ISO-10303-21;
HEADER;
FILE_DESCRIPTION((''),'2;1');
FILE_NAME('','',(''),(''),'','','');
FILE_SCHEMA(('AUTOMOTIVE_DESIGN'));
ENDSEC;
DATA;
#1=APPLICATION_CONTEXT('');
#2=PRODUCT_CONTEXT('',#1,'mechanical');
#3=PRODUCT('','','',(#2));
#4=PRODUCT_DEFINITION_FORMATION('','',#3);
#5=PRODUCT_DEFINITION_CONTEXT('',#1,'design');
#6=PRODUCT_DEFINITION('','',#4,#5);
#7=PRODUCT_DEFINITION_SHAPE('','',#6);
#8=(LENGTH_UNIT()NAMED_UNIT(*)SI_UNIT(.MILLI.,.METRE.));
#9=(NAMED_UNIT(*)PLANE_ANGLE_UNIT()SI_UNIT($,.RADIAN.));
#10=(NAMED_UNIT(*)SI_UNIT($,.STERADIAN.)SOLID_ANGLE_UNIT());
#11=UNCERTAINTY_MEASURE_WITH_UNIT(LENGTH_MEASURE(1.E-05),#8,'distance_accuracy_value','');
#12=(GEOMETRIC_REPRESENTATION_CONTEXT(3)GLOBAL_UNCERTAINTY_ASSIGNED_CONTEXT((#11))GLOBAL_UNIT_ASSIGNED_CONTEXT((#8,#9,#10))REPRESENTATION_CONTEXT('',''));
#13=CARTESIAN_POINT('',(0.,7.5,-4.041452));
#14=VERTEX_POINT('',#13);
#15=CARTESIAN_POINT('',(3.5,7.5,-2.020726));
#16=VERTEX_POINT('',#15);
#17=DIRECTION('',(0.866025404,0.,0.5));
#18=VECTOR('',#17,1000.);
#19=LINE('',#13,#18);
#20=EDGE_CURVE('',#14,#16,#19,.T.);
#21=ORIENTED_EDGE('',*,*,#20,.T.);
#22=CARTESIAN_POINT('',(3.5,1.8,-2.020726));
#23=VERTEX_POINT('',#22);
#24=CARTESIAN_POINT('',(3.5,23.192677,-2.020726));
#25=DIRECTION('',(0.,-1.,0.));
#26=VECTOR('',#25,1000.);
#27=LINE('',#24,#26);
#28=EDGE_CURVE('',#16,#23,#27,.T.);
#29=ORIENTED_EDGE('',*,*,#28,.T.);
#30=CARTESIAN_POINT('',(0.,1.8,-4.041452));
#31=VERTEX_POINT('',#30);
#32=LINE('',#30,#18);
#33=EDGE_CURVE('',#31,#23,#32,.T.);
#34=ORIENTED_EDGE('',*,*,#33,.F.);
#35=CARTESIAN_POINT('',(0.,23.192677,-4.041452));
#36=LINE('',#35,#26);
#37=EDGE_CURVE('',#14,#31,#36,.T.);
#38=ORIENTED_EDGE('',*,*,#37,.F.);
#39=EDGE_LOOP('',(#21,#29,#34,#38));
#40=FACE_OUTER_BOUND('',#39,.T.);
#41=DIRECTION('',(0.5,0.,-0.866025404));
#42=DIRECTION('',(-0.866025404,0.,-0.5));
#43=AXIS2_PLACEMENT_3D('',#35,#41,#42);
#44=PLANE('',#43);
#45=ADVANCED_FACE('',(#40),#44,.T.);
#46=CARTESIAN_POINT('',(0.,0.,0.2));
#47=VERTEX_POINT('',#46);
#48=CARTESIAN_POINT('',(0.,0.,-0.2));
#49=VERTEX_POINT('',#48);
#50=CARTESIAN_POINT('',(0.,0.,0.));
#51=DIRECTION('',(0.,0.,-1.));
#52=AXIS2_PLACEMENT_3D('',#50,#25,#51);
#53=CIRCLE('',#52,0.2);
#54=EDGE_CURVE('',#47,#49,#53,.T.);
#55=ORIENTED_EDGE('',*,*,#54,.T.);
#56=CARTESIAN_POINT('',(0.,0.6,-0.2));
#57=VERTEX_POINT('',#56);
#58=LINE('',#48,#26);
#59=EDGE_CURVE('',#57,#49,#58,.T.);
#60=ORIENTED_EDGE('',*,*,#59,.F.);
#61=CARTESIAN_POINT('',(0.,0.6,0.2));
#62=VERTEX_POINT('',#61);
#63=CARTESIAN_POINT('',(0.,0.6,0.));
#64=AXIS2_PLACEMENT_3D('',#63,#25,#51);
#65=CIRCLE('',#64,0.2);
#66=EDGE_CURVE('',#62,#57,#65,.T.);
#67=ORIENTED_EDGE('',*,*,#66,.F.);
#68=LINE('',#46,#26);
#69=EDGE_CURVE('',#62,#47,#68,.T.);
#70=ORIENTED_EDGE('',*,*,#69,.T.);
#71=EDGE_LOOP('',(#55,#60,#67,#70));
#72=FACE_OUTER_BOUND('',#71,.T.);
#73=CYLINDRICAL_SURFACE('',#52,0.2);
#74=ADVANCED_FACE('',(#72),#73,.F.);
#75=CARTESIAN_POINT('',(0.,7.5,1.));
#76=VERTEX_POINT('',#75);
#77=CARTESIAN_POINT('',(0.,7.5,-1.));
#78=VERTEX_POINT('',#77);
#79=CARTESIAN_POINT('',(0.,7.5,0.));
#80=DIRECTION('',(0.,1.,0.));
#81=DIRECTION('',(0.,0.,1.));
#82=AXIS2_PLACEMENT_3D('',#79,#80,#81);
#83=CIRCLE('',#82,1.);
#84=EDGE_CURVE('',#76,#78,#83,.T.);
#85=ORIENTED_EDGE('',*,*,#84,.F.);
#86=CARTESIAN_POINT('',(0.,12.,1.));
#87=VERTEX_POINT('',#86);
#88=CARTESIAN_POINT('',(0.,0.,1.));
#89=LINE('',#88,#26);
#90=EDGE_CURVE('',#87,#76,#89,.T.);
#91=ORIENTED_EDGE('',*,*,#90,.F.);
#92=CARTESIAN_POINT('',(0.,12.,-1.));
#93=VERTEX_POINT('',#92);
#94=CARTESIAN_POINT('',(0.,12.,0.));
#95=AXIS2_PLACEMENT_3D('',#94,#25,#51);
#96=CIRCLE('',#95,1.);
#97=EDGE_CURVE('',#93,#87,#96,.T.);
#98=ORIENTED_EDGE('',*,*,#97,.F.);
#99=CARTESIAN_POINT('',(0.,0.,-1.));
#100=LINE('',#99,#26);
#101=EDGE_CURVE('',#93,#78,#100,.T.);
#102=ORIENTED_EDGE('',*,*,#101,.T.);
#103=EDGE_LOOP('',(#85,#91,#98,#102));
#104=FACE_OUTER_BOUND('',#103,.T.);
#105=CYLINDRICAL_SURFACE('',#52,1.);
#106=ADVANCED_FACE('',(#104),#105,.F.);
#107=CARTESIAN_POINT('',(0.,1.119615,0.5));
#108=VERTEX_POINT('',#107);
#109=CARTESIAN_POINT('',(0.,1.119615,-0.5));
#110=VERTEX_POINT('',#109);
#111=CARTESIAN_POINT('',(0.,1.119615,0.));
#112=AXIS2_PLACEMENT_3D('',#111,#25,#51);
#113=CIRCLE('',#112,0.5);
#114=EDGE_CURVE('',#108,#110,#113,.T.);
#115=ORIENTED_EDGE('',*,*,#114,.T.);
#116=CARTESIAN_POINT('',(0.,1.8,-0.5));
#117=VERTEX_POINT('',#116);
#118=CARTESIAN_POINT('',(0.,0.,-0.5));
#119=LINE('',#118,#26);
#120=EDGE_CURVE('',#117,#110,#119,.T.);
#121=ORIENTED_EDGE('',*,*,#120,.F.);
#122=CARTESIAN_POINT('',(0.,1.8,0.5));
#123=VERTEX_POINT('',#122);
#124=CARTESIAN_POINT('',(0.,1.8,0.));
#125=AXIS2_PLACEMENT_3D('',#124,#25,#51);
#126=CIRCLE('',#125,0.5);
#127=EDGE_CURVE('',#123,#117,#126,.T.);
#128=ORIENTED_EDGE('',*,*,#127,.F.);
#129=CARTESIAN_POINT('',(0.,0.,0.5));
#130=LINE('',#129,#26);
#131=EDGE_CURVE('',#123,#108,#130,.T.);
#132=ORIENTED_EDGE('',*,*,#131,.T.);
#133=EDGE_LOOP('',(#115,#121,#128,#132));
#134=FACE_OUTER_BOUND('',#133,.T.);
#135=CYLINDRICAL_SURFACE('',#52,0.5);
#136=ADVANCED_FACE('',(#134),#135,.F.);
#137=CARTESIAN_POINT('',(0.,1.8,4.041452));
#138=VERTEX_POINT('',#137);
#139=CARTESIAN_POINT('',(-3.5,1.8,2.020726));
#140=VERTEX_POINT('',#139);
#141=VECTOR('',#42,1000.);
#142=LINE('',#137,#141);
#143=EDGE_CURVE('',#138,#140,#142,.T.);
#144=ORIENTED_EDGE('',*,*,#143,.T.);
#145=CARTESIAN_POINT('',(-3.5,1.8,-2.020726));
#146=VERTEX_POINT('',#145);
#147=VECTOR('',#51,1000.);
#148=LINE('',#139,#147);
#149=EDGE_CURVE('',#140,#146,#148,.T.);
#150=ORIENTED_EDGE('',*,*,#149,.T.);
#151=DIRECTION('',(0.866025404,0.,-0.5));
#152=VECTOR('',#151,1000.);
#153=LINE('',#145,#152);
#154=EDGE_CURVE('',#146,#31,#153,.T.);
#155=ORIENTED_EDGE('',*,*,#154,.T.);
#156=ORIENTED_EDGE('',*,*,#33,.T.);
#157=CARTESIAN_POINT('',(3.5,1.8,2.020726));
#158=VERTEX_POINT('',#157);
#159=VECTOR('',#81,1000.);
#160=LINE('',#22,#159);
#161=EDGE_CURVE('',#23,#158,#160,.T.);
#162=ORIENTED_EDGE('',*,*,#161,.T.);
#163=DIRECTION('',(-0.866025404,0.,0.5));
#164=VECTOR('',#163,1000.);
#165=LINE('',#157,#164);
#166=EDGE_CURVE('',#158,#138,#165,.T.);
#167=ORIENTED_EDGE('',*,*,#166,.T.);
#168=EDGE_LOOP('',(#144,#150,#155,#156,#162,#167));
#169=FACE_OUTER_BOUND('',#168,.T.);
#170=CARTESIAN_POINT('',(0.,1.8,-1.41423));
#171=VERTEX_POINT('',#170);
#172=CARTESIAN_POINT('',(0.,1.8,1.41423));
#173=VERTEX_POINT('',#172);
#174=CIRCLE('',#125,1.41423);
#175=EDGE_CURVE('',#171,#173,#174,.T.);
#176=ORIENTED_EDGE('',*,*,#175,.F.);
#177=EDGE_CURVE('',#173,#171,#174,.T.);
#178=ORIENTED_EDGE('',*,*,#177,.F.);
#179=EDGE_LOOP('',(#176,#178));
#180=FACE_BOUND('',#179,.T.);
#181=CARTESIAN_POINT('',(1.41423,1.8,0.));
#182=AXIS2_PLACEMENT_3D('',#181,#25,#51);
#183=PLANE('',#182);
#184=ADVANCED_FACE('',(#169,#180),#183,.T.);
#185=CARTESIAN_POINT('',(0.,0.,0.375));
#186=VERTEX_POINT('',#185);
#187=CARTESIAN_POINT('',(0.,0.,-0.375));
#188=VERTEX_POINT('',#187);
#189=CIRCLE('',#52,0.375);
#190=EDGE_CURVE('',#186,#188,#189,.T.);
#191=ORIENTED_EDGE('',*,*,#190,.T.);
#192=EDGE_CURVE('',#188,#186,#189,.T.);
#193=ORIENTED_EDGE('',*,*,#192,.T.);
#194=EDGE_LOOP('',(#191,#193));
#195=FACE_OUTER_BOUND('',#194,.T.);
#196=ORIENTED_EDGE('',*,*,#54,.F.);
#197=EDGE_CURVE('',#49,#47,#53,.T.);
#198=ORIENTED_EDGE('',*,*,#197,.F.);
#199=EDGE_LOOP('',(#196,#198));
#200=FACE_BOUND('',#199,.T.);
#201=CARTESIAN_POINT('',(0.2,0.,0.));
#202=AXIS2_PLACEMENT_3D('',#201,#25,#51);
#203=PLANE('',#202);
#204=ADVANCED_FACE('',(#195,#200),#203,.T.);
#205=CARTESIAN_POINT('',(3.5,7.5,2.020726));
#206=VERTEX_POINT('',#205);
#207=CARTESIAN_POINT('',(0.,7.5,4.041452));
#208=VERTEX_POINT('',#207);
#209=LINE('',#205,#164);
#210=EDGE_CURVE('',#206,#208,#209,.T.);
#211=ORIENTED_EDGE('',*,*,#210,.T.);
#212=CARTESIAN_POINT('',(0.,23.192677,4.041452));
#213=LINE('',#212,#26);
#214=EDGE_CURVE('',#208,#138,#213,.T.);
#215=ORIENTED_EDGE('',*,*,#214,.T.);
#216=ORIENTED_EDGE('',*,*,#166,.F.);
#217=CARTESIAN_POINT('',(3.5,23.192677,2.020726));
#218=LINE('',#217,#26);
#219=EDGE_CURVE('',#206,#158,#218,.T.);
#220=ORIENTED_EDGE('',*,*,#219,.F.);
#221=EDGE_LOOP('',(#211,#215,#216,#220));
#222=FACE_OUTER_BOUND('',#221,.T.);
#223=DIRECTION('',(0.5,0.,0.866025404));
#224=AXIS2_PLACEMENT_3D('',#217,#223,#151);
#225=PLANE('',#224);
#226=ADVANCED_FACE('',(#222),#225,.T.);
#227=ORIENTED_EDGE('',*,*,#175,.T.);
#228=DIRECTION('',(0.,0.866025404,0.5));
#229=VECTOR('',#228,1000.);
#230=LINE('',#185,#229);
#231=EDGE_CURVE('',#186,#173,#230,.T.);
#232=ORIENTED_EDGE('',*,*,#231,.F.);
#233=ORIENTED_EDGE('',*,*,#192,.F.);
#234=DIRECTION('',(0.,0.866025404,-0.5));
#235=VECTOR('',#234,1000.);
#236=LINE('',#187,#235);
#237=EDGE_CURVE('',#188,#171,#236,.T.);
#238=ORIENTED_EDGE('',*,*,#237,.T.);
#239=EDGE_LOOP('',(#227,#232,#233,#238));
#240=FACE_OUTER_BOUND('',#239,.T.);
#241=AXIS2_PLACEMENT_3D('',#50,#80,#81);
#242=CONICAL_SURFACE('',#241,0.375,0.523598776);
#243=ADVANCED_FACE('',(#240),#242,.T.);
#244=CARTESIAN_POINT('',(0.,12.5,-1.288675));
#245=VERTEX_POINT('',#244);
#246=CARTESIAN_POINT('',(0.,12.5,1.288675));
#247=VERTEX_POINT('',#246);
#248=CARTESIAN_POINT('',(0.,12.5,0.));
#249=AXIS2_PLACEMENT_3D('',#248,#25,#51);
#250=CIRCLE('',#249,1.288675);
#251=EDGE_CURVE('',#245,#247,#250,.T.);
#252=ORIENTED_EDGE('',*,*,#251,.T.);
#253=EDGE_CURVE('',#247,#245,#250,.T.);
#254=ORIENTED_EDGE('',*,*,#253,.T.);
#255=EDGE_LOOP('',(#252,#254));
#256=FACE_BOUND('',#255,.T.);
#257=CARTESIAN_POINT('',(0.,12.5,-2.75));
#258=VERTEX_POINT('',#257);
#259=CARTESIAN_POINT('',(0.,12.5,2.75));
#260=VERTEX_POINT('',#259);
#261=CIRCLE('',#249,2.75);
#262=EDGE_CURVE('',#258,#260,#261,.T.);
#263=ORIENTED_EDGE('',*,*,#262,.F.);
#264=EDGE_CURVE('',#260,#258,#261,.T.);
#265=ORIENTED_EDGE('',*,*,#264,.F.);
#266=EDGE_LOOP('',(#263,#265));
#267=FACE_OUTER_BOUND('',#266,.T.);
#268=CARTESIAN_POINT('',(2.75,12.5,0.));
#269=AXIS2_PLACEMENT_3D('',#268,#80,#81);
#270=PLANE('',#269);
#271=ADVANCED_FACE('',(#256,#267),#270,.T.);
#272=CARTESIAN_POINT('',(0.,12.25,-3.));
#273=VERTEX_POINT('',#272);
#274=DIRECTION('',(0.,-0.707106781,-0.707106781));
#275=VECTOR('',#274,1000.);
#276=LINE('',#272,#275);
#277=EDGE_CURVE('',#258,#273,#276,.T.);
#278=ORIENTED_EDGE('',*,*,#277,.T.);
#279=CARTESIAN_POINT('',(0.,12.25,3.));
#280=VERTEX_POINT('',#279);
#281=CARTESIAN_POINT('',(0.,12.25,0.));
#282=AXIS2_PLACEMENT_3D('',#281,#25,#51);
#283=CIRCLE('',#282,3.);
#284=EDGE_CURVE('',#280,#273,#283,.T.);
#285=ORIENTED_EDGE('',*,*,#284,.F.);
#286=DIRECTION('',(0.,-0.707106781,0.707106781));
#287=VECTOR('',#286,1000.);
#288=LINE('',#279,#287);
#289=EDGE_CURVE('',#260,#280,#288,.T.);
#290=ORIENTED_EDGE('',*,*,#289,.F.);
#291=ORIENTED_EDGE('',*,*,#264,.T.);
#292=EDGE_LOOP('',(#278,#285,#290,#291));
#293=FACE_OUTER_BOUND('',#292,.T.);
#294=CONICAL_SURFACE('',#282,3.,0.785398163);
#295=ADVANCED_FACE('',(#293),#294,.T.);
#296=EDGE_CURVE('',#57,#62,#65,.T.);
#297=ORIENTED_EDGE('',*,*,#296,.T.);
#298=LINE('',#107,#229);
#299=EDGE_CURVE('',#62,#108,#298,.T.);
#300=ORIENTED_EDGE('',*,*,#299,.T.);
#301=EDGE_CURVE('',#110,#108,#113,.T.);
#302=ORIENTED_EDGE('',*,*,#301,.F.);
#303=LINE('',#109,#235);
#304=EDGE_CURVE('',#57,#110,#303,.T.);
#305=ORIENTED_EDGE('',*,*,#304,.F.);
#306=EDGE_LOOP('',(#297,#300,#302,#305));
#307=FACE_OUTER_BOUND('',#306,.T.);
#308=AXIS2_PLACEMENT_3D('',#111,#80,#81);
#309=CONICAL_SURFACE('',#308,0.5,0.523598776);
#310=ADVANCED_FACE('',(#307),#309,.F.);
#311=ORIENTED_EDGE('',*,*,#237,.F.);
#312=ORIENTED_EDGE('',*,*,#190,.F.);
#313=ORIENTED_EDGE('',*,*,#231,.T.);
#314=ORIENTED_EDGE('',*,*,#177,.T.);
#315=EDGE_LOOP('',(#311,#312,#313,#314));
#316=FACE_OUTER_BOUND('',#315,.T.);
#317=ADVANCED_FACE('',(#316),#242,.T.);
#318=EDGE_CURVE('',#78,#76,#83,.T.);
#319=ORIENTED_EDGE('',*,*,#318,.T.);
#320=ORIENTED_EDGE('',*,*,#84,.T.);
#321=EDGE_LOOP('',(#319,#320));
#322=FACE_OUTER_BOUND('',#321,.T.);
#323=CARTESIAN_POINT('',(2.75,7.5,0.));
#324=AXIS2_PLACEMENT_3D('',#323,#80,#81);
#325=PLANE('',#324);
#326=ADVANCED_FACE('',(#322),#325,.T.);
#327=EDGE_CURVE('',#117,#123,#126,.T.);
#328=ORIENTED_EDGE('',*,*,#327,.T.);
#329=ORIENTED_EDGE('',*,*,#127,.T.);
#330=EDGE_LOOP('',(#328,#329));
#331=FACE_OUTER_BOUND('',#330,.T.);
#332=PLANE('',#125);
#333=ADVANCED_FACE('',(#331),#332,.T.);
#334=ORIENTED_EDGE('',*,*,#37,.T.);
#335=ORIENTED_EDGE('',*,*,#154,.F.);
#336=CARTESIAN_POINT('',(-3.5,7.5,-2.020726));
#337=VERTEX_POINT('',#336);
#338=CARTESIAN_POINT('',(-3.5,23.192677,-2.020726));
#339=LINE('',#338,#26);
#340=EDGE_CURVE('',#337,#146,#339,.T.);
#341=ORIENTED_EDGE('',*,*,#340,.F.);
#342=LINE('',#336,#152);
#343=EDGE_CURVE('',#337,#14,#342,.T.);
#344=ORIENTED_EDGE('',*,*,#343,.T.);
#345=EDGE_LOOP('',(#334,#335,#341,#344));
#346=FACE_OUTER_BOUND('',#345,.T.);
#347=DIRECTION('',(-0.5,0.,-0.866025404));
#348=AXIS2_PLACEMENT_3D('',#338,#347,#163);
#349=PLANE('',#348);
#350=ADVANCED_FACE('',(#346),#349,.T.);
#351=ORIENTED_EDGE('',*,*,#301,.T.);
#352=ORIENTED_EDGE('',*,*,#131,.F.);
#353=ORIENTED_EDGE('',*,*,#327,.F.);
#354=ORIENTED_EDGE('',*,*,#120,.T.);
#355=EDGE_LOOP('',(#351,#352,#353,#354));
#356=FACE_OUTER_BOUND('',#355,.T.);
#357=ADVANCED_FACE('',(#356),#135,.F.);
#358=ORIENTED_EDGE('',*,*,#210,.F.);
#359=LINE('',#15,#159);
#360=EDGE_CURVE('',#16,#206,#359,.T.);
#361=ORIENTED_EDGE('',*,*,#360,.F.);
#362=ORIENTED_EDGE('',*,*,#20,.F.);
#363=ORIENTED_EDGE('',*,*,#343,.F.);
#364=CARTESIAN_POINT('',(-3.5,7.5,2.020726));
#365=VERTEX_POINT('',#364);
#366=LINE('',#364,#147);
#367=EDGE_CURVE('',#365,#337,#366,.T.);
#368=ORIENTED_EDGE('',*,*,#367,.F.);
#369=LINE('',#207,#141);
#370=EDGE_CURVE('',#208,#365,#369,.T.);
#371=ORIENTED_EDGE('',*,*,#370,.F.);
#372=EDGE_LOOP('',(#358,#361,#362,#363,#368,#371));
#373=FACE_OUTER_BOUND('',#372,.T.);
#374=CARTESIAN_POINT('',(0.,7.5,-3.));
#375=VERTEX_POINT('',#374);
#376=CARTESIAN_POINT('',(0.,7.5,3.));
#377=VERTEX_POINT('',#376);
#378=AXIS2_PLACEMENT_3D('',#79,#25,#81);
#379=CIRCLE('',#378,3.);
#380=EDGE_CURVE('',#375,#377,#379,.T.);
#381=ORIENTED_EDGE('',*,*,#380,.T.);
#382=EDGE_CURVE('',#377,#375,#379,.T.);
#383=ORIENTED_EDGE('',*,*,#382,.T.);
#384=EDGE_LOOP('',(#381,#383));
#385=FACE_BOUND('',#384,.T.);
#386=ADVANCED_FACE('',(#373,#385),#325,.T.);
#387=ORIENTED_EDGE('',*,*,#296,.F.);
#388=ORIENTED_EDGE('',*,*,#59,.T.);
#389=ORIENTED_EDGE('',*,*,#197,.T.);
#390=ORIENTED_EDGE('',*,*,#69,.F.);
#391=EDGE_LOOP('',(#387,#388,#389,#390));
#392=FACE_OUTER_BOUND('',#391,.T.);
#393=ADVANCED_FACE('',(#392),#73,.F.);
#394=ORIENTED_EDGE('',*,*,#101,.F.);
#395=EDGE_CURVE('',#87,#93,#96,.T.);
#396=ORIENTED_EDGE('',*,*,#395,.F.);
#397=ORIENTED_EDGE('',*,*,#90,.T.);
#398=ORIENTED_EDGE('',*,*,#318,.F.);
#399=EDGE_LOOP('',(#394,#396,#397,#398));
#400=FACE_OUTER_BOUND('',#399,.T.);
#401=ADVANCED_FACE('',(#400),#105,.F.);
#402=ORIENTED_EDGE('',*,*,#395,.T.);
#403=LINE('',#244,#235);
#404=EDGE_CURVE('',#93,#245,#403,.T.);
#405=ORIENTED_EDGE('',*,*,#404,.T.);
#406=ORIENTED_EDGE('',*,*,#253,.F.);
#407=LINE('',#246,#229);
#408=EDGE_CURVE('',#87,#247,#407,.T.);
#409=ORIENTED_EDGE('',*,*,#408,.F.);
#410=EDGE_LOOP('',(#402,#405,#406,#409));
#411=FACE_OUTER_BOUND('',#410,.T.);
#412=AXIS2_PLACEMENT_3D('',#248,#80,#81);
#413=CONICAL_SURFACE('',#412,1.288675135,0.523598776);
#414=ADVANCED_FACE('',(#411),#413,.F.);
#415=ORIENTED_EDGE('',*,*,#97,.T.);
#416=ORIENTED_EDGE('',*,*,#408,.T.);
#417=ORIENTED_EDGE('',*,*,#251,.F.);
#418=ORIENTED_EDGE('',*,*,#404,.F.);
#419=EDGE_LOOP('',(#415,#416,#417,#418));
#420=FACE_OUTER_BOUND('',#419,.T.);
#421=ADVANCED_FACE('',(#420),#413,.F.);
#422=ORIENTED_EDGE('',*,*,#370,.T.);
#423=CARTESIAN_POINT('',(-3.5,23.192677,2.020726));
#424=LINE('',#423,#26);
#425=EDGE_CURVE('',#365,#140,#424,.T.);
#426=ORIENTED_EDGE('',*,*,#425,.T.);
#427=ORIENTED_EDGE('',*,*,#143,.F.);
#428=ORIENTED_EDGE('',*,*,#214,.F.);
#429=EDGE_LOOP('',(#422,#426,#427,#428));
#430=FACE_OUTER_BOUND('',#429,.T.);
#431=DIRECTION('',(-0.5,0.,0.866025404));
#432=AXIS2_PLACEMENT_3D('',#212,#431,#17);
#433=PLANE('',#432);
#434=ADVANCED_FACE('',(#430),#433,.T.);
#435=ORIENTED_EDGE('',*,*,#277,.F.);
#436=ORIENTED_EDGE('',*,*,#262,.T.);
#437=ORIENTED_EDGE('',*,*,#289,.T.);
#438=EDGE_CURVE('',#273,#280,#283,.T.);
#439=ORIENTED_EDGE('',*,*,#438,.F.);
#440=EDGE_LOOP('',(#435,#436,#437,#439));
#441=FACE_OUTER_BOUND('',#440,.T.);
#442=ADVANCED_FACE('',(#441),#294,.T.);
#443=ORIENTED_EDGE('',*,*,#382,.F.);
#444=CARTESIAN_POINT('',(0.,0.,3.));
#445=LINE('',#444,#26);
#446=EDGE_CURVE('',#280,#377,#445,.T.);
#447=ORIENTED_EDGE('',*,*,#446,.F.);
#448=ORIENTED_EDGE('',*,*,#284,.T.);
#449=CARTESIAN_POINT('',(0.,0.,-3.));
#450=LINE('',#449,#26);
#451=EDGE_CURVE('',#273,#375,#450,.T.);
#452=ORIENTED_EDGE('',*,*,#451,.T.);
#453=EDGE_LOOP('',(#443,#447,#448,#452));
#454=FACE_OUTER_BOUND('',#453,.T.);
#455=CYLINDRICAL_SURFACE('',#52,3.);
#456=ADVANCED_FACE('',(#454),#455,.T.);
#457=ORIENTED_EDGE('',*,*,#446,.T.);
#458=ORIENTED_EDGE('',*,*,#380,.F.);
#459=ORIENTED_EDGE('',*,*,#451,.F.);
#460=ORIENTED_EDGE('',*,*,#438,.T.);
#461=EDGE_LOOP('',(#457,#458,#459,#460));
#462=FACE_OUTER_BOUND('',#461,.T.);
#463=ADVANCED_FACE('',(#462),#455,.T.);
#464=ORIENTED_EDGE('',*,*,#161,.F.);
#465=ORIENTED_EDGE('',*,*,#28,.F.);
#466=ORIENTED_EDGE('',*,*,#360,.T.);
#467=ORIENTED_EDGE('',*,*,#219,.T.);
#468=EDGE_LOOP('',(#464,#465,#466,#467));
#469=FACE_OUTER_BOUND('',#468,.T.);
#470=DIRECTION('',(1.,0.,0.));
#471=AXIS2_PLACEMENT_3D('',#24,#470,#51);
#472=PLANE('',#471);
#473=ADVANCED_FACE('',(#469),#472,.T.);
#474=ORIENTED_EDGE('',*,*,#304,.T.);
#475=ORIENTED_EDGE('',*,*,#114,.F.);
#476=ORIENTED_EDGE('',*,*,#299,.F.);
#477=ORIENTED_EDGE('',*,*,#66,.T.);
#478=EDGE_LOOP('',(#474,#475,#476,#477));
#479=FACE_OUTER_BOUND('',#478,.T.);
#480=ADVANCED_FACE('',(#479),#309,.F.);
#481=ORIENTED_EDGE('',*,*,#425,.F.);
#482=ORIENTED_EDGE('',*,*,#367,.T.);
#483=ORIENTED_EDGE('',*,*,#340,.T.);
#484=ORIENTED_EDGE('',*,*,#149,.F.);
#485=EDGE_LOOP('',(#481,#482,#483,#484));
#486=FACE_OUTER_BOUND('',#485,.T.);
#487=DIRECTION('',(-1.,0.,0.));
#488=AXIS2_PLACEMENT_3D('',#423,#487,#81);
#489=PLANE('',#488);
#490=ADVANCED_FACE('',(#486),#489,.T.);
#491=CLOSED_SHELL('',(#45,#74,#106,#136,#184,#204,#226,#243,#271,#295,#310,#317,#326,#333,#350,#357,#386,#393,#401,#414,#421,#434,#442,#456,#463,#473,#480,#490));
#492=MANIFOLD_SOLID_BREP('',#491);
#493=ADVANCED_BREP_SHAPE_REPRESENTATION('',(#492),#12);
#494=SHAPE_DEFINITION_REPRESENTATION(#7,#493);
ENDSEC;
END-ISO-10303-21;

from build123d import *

# Parameters (mm, degrees)
BOSS_EXTRUDE1_DEPTH = 5.7


with BuildPart() as part:
    # Sketch1 → Revolve1 (revolve)
    with BuildSketch(Plane.XY, mode=Mode.PRIVATE) as revolve1_sk:
        Polygon((0.2, 0), (0.375, 0), (1.414230485, 1.8), (2.5, 1.8), (2.5, 6.5), (3, 7.366025404), (3, 12.25), (2.75, 12.5), (1.288675135, 12.5), (1, 12), (1, 3.985640646), (0.5, 3.119615242), (0.5, 1.119615242), (0.2, 0.6), align=None)
    revolve(revolve1_sk.sketch.rotate(Axis((0, 0, 0), (0, 1, 0)), 90), axis=Axis((0, 0, 0), (0, 1, 0)))

    # Sketch2 → Boss-Extrude1 (add)
    with BuildSketch(Plane.XZ.offset(-1.8)):
        Polygon((0, 4.041451884), (-3.5, 2.020725942), (-3.5, -2.020725942), (0, -4.041451884), (3.5, -2.020725942), (3.5, 2.020725942), align=None)
    extrude(amount=-BOSS_EXTRUDE1_DEPTH)


solid = part.part
